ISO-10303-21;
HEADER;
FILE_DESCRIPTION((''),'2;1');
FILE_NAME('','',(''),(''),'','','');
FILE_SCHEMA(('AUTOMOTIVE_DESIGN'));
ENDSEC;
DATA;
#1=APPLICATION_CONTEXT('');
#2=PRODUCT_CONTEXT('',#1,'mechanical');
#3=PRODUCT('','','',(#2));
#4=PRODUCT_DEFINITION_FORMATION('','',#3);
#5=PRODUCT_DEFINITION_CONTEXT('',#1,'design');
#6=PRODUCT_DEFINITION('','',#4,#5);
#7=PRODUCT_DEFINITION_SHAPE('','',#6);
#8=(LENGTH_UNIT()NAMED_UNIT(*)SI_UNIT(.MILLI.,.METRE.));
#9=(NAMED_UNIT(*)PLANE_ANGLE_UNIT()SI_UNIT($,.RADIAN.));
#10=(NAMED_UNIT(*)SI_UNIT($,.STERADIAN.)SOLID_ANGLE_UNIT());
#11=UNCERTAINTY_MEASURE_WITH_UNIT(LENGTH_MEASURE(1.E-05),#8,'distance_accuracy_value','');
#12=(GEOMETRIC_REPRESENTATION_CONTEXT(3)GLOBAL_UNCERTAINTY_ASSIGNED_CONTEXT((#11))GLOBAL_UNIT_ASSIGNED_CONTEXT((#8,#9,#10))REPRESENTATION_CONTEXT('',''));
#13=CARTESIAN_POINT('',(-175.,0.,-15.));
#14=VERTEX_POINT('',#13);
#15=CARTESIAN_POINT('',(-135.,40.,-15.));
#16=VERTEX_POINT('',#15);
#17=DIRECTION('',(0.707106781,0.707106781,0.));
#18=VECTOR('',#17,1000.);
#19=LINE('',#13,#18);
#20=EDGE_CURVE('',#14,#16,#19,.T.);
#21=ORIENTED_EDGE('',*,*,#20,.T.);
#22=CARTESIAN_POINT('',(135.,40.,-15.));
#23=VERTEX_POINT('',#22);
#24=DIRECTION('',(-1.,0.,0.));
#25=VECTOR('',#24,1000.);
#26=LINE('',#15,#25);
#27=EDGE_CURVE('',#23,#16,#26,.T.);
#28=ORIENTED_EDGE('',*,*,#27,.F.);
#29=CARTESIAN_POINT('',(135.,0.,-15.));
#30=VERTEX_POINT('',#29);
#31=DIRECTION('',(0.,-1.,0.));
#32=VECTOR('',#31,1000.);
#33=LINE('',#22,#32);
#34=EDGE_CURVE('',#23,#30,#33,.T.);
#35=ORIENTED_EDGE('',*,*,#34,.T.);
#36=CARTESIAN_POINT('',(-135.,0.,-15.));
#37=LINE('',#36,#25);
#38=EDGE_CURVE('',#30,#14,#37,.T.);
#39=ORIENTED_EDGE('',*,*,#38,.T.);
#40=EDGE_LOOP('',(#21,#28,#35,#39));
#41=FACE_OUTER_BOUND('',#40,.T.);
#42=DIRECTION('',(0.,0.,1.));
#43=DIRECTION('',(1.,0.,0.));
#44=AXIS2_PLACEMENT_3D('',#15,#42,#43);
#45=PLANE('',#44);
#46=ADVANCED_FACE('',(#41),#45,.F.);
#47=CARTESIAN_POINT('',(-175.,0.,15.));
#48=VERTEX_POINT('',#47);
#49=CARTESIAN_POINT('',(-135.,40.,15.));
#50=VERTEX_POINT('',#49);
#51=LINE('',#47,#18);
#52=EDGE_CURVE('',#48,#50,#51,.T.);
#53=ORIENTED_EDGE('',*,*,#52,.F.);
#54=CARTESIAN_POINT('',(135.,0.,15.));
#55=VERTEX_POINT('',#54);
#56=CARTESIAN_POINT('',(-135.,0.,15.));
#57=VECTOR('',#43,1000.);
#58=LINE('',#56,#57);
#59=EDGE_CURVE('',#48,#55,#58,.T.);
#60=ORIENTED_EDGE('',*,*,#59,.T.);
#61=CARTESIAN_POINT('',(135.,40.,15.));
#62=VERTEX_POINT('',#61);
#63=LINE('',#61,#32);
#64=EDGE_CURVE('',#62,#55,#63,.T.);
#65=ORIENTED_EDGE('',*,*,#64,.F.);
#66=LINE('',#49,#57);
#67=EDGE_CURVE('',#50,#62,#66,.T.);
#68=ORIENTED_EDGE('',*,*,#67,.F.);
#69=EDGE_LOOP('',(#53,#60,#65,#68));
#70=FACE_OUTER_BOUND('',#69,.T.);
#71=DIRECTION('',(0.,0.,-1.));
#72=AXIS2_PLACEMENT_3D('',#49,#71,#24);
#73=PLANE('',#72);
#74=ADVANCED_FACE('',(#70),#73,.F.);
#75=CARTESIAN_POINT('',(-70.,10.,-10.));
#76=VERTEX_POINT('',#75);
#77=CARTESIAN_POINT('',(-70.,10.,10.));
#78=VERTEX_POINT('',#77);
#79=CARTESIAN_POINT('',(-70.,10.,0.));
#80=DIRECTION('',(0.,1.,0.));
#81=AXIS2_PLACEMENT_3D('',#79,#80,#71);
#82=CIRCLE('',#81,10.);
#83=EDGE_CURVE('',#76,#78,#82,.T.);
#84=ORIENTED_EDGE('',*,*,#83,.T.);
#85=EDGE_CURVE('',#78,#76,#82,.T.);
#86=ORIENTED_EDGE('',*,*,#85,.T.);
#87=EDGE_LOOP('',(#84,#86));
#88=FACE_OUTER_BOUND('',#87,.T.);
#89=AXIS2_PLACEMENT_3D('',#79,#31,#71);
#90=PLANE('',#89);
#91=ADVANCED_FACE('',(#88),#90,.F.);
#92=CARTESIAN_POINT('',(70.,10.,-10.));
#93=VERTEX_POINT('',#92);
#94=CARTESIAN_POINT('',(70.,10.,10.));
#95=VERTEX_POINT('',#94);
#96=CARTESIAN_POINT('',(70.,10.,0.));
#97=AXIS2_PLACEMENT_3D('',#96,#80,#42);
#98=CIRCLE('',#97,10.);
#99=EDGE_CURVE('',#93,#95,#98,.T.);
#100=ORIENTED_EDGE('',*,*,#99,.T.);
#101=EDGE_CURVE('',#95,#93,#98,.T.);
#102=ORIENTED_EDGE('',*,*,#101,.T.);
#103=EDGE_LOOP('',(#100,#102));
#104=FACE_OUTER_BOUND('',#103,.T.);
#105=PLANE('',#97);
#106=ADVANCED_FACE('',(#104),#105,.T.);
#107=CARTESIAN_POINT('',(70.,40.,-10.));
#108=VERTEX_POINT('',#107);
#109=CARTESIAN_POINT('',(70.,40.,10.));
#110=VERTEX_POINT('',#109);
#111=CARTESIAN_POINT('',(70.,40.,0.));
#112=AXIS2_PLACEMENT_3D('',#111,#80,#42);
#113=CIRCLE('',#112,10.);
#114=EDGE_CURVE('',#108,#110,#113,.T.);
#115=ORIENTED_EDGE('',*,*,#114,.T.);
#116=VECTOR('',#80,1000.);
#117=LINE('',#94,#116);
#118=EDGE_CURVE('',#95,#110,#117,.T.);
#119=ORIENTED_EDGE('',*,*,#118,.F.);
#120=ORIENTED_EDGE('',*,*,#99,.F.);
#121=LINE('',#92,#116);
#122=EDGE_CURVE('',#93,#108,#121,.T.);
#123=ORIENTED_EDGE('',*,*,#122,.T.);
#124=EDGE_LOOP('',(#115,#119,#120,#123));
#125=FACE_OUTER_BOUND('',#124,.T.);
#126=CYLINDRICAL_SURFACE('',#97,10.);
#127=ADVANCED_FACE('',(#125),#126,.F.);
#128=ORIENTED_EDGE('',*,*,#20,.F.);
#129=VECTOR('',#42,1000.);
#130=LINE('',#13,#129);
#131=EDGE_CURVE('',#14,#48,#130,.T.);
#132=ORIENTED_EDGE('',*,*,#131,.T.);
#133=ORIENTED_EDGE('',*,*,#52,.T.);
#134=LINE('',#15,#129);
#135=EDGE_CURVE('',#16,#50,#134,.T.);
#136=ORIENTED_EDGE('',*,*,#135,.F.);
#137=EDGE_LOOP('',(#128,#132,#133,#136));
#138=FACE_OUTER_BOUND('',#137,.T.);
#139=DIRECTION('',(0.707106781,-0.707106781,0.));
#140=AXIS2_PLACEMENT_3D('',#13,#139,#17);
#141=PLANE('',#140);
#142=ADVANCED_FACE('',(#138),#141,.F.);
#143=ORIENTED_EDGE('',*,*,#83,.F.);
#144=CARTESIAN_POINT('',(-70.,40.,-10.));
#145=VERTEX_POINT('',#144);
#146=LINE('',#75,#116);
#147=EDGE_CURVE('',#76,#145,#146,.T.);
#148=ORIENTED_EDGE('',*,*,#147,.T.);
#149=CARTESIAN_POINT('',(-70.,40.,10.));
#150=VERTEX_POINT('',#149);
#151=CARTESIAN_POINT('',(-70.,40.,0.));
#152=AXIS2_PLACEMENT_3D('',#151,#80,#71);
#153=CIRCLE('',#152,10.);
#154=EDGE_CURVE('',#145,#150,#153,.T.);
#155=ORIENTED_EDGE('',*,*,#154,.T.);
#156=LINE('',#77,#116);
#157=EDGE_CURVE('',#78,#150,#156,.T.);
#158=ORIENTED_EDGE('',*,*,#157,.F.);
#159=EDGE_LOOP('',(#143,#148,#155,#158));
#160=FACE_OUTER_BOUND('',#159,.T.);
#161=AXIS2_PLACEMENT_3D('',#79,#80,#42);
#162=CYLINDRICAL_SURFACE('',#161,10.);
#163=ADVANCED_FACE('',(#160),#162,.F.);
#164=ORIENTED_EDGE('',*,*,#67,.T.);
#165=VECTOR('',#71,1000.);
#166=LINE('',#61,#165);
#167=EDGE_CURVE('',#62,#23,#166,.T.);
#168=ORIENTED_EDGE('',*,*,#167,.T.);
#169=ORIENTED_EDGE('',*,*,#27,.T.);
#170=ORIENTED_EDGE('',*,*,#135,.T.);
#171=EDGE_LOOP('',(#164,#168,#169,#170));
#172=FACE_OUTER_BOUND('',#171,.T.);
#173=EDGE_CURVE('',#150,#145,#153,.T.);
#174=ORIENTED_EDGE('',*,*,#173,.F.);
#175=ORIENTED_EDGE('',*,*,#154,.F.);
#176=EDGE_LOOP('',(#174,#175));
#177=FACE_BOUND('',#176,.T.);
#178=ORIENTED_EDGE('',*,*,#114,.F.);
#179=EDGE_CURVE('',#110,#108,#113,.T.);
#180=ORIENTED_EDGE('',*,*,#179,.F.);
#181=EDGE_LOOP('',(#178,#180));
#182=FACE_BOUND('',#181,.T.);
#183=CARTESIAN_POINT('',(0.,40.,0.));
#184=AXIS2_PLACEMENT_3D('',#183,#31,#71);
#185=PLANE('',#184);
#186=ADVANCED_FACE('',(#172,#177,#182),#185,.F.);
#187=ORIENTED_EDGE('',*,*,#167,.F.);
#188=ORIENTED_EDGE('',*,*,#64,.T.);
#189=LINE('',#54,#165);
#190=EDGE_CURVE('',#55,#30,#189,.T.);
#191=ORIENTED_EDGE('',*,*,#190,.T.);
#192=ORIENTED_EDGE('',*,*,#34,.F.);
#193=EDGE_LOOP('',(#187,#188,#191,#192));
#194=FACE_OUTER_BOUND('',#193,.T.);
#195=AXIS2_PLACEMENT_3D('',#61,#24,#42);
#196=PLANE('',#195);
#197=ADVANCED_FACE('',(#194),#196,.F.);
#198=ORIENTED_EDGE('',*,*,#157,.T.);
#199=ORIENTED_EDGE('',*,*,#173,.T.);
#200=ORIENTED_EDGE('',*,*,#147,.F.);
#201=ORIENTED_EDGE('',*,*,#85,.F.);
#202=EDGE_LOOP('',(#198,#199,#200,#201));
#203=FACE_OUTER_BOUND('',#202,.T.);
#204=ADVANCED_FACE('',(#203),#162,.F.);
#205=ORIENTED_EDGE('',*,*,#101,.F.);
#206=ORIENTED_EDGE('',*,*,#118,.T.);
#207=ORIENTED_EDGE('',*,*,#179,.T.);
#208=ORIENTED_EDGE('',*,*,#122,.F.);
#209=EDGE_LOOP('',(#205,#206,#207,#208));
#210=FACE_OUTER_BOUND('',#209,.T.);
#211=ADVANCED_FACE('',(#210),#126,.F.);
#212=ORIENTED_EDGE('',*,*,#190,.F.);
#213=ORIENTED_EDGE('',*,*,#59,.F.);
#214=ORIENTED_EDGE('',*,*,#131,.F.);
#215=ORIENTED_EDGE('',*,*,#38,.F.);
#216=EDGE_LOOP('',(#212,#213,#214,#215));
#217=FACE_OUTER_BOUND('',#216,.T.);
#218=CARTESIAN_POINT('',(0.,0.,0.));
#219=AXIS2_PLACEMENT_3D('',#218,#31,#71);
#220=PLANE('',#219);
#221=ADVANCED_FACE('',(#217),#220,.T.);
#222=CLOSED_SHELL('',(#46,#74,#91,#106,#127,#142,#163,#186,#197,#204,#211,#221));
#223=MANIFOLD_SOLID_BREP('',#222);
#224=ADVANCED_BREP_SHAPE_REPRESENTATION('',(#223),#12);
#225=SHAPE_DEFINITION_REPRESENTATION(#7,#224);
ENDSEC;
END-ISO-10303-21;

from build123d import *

# Parameters (mm, degrees)
SKETCH_1_W          = 270
SKETCH_1_H          = 30
EXTRUDE_1_DEPTH     = 40
SKETCH_2_R          = 10
CUT_EXTRUDE_2_DEPTH = 30
SKETCH_3_W          = 30
SKETCH_3_H          = 40
EXTRUDE_2_DEPTH     = 40
CUT_EXTRUDE_3_DEPTH = 183.002747232


with BuildPart() as part:
    # 草图1 → 凸台-拉伸1 (new body)
    with BuildSketch(Plane(origin=(0, 0, 0), x_dir=(1, 0, 0), z_dir=(0, 1, 0))):
        Rectangle(SKETCH_1_W, SKETCH_1_H)
    extrude(amount=EXTRUDE_1_DEPTH)

    # 草图2 → 切除-拉伸2 (cut)
    with BuildSketch(Plane(origin=(0, 40, 0), x_dir=(1, 0, 0), z_dir=(0, 1, 0))):
        with Locations(Location((70, 0, 0), (0, 0, 270))):
            Circle(SKETCH_2_R)
        with Locations(Location((-70, 0, 0), (0, 0, 90))):
            Circle(SKETCH_2_R)
    extrude(amount=-CUT_EXTRUDE_2_DEPTH, mode=Mode.SUBTRACT)

    # 草图3 → 凸台-拉伸2 (add)
    with BuildSketch(Plane.ZY.offset(135)):
        with Locations((0, 20)):
            Rectangle(SKETCH_3_W, SKETCH_3_H)
    extrude(amount=EXTRUDE_2_DEPTH)

    # 草图4 → 切除-拉伸3 (cut, through all)
    with BuildSketch(Plane.XY.offset(15)):
        Polygon((-175, 0), (-135, 40), (-175, 40), align=None)
    extrude(amount=-CUT_EXTRUDE_3_DEPTH, mode=Mode.SUBTRACT)


solid = part.part
